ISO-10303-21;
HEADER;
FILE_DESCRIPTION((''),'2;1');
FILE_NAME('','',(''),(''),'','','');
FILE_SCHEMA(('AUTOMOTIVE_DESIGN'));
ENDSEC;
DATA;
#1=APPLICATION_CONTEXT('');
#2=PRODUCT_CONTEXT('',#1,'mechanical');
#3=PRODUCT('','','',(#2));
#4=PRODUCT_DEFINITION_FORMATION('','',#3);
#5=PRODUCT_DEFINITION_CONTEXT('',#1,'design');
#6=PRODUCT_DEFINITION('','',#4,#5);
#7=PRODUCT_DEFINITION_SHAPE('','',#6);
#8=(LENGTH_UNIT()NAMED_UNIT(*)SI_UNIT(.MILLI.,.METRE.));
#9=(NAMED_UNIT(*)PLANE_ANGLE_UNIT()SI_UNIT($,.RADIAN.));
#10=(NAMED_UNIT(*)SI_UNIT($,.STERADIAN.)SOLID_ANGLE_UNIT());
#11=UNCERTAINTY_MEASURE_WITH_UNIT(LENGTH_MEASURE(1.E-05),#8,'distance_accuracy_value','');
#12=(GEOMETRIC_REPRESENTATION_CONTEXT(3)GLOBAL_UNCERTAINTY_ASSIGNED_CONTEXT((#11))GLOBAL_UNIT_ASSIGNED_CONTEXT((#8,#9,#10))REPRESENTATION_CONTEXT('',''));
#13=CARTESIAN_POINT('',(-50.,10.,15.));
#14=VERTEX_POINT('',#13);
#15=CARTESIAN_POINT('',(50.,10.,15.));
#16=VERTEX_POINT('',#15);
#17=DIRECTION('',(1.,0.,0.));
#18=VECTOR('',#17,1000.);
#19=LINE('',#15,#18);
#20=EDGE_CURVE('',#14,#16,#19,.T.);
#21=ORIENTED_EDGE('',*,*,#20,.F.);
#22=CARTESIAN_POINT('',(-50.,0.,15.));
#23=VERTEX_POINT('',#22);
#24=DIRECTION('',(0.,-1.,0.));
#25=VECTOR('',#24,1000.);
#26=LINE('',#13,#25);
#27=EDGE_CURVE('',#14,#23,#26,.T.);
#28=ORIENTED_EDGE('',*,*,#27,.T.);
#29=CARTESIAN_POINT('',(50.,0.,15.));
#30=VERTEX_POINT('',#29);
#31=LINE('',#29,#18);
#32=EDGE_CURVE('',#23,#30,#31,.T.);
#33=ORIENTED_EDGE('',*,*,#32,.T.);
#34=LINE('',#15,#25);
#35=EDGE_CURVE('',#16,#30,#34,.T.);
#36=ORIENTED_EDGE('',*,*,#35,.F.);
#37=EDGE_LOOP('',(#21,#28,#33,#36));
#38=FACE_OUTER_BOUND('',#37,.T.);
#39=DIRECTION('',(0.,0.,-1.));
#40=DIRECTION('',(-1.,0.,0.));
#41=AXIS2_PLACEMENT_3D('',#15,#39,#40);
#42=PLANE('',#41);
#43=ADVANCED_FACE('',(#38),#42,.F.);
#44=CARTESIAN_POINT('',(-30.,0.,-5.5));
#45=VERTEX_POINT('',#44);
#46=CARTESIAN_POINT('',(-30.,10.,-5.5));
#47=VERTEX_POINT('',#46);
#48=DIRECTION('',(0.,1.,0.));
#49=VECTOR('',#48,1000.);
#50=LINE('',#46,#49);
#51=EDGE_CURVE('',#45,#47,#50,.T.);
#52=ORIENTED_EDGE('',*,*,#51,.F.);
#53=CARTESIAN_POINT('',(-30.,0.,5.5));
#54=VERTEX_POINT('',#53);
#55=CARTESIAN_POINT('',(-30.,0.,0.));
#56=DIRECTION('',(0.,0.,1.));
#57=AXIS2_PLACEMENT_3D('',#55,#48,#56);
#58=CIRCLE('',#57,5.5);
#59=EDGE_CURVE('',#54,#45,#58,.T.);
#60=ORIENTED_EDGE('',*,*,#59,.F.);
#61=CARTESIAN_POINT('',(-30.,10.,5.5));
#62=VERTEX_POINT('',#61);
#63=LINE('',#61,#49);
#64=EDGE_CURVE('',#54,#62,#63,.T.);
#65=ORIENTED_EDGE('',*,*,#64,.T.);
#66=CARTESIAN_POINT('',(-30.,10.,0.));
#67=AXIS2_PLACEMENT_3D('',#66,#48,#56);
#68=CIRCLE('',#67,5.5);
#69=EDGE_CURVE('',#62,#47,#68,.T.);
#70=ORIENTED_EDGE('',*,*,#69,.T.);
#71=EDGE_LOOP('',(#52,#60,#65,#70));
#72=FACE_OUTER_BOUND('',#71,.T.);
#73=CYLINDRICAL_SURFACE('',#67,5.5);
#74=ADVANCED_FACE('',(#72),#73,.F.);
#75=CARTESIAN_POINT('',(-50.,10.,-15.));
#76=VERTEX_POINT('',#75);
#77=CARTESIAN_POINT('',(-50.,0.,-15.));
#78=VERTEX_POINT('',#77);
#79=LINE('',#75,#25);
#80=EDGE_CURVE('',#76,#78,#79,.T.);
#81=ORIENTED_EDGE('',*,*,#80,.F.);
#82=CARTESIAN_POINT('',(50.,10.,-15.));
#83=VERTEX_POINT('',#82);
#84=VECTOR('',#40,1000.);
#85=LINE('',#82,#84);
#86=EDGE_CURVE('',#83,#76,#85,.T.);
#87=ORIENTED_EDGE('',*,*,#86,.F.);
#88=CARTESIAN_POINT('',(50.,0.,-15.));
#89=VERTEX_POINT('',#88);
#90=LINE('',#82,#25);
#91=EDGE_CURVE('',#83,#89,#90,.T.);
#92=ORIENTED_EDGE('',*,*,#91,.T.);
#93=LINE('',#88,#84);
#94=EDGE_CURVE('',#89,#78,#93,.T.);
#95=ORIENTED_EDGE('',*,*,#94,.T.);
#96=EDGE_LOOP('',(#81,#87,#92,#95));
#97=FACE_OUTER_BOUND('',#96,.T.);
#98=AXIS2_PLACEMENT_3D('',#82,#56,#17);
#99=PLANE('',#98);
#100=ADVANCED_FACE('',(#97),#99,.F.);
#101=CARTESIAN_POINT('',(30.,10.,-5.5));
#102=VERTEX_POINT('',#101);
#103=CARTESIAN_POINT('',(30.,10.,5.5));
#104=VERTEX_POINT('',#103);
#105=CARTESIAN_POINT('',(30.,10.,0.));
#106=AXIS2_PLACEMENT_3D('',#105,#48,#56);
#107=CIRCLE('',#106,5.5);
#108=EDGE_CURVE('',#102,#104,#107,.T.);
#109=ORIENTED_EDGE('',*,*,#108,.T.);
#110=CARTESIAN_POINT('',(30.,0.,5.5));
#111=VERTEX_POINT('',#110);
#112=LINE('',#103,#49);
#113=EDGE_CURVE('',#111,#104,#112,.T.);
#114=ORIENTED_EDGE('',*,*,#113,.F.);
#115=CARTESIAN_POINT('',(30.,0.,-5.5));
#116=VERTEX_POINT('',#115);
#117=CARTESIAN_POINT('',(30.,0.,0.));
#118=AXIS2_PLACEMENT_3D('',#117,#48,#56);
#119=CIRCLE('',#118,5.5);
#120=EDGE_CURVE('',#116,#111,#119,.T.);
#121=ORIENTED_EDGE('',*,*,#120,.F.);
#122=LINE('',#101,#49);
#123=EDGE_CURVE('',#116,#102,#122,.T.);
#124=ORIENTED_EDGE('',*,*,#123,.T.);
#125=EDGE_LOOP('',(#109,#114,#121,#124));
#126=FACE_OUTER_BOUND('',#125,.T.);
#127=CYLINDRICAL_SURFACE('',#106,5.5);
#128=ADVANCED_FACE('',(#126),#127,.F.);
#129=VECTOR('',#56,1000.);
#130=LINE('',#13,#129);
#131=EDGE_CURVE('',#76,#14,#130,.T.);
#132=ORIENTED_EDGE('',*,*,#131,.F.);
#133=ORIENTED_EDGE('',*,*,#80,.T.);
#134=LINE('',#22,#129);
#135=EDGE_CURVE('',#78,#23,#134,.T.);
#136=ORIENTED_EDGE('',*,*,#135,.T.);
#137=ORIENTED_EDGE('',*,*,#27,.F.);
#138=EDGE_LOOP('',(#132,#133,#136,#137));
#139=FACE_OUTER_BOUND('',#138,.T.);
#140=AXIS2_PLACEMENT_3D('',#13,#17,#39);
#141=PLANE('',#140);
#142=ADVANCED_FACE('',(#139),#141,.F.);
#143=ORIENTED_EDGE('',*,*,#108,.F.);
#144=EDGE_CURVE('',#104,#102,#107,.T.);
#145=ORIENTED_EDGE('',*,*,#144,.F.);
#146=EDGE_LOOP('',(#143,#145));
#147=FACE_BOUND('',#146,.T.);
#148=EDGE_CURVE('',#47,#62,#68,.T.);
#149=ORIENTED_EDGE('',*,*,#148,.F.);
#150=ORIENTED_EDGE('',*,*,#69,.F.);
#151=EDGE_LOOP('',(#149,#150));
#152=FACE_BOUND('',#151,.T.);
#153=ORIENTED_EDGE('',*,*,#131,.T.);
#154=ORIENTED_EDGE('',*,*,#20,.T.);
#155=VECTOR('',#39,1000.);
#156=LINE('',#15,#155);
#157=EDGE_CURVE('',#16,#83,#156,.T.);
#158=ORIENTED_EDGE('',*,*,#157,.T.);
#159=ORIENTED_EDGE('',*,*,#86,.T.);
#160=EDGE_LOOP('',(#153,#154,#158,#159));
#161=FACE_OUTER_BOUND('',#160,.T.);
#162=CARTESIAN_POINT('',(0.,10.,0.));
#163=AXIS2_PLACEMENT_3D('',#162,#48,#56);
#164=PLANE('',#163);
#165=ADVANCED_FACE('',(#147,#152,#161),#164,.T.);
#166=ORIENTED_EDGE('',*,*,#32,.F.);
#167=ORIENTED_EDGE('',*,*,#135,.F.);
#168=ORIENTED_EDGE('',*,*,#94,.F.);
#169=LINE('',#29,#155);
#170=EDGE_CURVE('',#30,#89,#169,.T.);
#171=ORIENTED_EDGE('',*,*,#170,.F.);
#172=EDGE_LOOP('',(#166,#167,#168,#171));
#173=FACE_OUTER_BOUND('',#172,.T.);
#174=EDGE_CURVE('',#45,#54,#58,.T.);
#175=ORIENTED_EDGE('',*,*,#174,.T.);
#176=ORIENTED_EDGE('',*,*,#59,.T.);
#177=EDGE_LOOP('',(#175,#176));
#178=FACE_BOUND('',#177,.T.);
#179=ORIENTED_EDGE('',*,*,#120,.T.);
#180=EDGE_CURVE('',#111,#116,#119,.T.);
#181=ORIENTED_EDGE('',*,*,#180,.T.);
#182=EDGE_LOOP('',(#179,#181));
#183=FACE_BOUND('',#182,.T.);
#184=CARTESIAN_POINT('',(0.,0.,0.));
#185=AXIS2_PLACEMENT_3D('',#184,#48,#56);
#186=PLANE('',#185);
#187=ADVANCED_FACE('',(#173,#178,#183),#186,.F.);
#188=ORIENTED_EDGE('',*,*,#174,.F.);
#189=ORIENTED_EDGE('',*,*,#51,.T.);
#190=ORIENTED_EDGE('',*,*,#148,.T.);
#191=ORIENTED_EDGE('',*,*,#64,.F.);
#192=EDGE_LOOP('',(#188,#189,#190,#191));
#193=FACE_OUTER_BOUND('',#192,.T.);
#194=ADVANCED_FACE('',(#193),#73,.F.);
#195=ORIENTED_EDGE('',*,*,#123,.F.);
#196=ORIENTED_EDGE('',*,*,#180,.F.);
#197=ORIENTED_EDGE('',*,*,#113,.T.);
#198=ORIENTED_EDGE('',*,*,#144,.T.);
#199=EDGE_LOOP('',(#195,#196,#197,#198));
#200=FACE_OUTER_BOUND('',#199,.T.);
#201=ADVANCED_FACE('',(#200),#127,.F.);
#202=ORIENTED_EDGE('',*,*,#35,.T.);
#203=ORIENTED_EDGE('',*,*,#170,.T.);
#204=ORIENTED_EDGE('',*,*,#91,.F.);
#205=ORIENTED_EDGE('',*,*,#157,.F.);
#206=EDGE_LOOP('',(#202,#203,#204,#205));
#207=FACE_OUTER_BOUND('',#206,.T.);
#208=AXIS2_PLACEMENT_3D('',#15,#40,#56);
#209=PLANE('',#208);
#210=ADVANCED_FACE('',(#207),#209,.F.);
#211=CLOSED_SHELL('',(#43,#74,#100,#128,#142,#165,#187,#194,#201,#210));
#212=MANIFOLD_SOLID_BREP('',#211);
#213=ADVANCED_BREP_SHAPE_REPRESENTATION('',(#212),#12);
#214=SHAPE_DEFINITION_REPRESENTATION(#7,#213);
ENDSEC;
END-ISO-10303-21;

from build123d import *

# Parameters (mm, degrees)
SKETCH1_W                  = 100
SKETCH1_H                  = 30
BOSS_EXTRUDE1_DEPTH        = 10
F_11_0_11_DIAMETER_HOLE1_D = 11


with BuildPart() as part:
    # Sketch1 → Boss-Extrude1 (new body)
    with BuildSketch(Plane(origin=(0, 0, 0), x_dir=(1, 0, 0), z_dir=(0, 1, 0))):
        Rectangle(SKETCH1_W, SKETCH1_H)
    extrude(amount=BOSS_EXTRUDE1_DEPTH)

    # Ø11.0 (11) Diameter Hole1 (through all)
    with Locations(Plane(origin=(0, 10, 0), x_dir=(1, 0, 0), z_dir=(0, 1, 0))):
        with Locations((-30, 0), (30, 0)):
            Hole(F_11_0_11_DIAMETER_HOLE1_D / 2)


solid = part.part
